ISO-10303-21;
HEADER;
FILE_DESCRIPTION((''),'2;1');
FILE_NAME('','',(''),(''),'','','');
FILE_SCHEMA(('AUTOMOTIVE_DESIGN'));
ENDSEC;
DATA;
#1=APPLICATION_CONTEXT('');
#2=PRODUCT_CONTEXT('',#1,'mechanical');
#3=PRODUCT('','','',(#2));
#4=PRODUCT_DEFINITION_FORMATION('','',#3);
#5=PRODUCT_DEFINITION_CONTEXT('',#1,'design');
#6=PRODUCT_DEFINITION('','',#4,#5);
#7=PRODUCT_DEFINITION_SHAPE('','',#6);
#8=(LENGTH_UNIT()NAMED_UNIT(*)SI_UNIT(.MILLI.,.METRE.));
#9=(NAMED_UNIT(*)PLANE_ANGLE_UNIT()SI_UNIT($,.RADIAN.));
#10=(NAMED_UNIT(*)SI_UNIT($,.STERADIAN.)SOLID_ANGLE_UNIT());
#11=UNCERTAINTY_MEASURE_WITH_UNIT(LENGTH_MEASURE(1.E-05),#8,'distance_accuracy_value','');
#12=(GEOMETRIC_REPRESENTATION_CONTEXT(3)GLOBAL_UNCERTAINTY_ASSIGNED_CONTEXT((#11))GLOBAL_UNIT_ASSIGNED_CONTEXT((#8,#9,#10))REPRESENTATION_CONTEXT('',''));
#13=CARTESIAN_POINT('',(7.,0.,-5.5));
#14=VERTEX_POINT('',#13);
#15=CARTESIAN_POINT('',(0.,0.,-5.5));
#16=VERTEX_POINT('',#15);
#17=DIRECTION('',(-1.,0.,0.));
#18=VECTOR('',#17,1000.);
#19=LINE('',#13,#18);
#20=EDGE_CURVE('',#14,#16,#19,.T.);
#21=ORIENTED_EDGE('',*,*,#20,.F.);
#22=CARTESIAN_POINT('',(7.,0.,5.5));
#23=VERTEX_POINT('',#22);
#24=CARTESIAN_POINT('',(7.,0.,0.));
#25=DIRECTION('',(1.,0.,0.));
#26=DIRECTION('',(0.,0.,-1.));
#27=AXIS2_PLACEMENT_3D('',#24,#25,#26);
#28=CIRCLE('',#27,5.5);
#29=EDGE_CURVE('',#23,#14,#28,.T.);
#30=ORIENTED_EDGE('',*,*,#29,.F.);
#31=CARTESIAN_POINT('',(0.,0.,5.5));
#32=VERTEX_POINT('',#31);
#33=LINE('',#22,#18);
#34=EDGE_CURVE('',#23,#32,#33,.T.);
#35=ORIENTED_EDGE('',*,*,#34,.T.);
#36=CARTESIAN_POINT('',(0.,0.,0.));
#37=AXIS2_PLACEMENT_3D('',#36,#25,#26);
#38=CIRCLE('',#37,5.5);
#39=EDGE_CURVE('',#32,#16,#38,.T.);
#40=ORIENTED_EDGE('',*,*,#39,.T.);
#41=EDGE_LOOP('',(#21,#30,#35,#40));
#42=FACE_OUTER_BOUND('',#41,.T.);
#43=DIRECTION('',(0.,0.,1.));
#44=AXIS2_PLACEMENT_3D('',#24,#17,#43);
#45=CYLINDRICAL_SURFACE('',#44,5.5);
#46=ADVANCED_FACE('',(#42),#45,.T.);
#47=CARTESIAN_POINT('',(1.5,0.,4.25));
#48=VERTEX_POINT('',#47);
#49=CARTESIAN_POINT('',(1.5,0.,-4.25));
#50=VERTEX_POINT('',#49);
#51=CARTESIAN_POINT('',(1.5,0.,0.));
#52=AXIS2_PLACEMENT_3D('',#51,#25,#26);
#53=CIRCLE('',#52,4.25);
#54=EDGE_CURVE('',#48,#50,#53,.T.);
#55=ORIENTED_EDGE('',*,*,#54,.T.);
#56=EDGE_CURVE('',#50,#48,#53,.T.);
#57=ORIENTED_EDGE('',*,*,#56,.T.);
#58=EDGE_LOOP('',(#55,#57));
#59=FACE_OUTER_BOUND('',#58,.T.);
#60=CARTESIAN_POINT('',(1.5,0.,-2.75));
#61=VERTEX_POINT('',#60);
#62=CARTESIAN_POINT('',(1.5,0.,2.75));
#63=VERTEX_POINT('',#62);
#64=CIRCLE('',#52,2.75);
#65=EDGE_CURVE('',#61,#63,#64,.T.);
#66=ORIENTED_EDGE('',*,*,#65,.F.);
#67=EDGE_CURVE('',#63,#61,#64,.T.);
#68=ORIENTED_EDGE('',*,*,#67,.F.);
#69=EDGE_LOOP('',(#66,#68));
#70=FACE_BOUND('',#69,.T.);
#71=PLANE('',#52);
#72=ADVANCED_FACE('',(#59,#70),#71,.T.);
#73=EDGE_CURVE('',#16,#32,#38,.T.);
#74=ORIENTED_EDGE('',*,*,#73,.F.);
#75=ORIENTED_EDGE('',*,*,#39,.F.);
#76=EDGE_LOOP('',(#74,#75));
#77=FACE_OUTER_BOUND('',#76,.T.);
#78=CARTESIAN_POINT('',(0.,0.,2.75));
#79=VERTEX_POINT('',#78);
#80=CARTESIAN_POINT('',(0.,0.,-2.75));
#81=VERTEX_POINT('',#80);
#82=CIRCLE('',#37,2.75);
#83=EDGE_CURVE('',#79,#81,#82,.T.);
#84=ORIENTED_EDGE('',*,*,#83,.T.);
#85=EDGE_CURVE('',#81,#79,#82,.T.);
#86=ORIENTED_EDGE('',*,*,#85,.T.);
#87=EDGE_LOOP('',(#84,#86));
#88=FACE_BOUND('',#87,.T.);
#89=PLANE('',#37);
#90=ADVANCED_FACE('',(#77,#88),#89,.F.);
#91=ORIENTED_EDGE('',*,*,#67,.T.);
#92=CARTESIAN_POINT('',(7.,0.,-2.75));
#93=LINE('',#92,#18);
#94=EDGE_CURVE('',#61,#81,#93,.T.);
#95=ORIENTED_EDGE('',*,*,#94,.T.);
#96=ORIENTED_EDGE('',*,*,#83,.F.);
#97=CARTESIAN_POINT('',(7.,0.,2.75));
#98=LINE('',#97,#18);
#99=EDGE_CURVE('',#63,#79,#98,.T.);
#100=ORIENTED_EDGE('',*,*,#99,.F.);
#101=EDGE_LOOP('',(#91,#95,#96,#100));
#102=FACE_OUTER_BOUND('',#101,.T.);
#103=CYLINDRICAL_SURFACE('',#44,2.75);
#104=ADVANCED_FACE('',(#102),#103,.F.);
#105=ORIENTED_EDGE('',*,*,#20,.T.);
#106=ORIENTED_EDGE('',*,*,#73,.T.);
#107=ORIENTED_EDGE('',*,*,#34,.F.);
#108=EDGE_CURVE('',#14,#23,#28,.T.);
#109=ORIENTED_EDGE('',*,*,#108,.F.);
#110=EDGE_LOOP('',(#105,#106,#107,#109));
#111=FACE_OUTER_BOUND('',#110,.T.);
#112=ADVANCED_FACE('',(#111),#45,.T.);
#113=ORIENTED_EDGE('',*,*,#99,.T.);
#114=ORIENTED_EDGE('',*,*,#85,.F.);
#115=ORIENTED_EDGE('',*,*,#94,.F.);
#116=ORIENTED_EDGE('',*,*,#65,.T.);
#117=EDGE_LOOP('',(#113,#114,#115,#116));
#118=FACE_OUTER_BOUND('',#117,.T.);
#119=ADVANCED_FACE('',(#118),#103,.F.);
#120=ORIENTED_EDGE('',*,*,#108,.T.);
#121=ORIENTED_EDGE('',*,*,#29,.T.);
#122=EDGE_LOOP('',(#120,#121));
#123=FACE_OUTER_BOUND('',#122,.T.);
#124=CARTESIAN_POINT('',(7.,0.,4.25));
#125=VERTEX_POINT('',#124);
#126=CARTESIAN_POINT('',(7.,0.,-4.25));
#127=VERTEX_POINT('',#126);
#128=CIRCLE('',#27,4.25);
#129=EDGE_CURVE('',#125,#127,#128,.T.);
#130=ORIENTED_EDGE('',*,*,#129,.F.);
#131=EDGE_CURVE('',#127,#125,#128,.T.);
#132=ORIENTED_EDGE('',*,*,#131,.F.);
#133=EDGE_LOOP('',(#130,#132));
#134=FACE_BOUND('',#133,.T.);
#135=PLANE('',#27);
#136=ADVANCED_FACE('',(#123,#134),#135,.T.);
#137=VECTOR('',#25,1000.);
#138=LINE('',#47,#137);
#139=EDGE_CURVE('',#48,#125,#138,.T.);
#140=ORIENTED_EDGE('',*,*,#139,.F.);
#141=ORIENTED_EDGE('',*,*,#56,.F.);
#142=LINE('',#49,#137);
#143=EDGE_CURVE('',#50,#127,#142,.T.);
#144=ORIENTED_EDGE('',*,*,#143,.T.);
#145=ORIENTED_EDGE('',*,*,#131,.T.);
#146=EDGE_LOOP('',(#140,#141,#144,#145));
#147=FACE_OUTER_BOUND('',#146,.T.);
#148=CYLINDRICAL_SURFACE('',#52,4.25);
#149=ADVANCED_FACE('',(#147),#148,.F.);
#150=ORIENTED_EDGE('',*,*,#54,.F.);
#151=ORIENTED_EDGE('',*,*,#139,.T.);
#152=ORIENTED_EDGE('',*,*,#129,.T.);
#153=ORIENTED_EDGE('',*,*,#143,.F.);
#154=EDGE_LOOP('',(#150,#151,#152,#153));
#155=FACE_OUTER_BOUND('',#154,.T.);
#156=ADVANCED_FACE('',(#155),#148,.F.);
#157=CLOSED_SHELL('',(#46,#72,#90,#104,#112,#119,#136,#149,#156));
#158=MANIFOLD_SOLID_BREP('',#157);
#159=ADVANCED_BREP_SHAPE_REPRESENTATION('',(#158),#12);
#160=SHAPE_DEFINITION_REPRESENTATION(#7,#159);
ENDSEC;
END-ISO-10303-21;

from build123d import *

# Parameters (mm, degrees)
SKETCH1_R           = 5.5
SKETCH1_R_2         = 2.75
BOSS_EXTRUDE1_DEPTH = 7
SKETCH2_R           = 4.25
CUT_EXTRUDE1_DEPTH  = 5.5


with BuildPart() as part:
    # Sketch1 → Boss-Extrude1 (new body)
    with BuildSketch(Plane(origin=(0, 0, 0), x_dir=(0, 0, -1), z_dir=(1, 0, 0))):
        Circle(SKETCH1_R)
        Circle(SKETCH1_R_2, mode=Mode.SUBTRACT)
    extrude(amount=BOSS_EXTRUDE1_DEPTH)

    # Sketch2 → Cut-Extrude1 (cut)
    with BuildSketch(Plane(origin=(7, 0, 0), x_dir=(0, 0, -1), z_dir=(1, 0, 0))):
        Circle(SKETCH2_R)
    extrude(amount=-CUT_EXTRUDE1_DEPTH, mode=Mode.SUBTRACT)


solid = part.part
